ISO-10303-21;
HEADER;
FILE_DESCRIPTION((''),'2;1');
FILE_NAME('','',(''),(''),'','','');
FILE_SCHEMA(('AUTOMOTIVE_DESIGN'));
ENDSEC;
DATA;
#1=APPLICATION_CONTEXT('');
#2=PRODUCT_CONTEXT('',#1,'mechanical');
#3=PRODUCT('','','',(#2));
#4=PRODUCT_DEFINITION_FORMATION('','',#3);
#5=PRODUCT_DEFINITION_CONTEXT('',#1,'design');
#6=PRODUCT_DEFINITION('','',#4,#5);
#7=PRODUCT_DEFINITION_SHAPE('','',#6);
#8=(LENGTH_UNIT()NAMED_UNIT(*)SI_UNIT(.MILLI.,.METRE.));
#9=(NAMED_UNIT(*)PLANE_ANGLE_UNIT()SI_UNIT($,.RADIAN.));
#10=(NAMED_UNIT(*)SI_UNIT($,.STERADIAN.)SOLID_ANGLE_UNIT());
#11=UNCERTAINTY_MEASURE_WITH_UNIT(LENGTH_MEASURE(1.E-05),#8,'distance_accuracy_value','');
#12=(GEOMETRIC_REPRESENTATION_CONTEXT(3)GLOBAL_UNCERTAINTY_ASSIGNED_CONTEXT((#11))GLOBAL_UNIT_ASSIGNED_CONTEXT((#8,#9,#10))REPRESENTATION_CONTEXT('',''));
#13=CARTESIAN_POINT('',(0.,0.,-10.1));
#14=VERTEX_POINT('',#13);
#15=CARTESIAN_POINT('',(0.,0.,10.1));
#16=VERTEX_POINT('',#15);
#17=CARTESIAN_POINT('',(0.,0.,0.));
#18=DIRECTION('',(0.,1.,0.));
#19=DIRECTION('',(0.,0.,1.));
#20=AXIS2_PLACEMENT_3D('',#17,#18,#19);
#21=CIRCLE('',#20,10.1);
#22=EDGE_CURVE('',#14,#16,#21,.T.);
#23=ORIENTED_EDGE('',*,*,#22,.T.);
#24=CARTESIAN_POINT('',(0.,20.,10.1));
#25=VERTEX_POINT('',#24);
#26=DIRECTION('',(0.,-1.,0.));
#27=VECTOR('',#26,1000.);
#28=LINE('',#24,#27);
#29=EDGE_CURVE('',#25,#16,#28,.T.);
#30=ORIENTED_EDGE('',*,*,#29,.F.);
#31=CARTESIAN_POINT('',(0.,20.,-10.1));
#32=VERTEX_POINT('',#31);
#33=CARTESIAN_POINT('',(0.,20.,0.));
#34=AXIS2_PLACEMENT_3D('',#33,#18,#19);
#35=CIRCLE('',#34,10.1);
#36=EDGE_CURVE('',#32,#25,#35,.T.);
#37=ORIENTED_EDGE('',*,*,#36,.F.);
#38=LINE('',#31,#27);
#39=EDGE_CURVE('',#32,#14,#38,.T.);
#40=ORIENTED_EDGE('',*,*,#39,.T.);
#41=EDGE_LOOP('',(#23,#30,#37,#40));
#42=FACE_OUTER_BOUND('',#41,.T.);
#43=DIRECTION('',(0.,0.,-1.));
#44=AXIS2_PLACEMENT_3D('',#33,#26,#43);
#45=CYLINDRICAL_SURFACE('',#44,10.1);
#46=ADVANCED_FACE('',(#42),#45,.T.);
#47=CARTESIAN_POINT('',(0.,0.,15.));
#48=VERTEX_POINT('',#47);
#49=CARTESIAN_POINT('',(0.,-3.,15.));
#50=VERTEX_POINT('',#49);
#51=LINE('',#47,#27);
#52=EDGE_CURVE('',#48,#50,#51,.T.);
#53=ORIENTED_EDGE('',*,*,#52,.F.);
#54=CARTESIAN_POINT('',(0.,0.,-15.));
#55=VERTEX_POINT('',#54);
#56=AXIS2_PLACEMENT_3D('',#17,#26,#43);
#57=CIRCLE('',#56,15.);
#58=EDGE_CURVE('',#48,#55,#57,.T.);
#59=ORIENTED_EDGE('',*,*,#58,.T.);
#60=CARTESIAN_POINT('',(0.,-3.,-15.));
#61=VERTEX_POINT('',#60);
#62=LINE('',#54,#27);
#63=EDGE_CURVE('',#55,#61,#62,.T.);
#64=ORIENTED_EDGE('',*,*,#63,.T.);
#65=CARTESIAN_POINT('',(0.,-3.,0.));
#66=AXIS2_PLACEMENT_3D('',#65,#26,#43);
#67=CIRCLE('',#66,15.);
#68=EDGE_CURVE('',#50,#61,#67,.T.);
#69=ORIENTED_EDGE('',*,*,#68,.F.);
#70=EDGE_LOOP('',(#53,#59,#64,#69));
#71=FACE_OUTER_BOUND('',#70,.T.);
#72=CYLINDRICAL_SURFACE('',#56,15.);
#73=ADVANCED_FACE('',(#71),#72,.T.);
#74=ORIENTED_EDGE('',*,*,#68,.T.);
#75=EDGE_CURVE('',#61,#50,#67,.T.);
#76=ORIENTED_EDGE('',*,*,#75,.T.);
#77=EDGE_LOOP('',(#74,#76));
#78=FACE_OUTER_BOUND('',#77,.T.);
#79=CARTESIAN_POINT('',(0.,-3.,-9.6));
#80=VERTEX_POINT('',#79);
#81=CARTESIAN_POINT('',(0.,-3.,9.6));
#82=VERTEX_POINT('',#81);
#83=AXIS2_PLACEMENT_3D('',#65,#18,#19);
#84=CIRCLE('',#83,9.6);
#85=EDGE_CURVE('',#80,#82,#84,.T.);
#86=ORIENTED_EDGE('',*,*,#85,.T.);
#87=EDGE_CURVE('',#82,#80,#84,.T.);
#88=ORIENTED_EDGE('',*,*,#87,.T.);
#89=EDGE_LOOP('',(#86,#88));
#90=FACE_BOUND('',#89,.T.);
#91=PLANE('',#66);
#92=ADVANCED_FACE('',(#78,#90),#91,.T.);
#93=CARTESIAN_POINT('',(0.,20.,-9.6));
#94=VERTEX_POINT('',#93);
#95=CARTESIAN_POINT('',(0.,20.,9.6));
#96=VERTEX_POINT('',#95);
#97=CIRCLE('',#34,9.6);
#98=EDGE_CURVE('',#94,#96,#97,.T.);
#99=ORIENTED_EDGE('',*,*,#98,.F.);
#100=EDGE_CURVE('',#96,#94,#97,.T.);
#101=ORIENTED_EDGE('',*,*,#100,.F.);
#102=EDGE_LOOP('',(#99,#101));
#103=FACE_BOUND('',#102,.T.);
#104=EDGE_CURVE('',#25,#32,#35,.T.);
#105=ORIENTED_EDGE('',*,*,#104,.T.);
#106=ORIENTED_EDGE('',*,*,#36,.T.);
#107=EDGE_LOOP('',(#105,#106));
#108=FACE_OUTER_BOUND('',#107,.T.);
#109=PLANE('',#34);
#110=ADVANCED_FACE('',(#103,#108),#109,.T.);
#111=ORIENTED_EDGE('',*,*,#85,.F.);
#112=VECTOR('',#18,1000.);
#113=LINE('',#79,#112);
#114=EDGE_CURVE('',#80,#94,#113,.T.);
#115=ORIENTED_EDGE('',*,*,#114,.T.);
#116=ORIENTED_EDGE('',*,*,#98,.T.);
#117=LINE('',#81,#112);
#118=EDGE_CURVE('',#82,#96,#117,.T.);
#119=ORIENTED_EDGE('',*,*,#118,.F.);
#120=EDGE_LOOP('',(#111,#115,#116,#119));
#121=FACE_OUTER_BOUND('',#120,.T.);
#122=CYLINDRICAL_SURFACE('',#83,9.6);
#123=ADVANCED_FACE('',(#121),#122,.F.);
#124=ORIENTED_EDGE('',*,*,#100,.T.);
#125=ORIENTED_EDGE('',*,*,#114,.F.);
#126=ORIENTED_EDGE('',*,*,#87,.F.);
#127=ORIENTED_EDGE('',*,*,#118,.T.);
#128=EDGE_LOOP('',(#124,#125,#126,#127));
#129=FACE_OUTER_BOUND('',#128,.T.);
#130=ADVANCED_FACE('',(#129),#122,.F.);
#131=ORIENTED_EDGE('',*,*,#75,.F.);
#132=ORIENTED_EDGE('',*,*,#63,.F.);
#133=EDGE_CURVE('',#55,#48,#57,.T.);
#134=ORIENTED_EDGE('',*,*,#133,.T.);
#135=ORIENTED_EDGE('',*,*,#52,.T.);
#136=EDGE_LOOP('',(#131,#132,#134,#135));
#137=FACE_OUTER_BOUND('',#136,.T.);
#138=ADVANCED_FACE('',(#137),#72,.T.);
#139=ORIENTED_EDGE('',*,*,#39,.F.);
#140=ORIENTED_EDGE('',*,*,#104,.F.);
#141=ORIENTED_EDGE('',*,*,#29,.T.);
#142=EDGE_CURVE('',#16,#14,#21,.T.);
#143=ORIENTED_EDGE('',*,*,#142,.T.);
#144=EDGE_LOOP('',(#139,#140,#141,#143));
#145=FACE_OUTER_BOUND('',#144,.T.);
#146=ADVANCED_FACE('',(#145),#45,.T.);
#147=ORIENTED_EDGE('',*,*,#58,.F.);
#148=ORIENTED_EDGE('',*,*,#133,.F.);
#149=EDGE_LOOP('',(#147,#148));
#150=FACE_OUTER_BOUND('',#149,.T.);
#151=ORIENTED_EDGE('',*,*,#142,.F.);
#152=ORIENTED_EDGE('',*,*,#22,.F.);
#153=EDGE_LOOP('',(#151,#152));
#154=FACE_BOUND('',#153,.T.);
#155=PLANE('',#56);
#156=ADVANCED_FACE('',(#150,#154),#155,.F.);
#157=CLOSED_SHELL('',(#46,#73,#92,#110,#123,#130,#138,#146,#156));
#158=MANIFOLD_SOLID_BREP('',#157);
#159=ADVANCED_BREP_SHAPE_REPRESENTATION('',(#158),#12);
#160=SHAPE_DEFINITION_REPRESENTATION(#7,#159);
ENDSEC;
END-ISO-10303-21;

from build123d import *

# Parameters (mm, degrees)
SKETCH1_R           = 10.1
BOSS_EXTRUDE1_DEPTH = 20
BOSS_EXTRUDE2_START = 3
SKETCH2_R           = 15
BOSS_EXTRUDE2_DEPTH = 3
SKETCH4_R           = 9.6
CUT_EXTRUDE1_DEPTH  = 32.288975694


with BuildPart() as part:
    # Sketch1 → Boss-Extrude1 (new body)
    with BuildSketch(Plane(origin=(0, 0, 0), x_dir=(1, 0, 0), z_dir=(0, 1, 0))):
        with Locations(Location((0, 0, 0), (0, 0, 270))):
            Circle(SKETCH1_R)
    extrude(amount=BOSS_EXTRUDE1_DEPTH)

    # Sketch2 → Boss-Extrude2 (add)
    with BuildSketch(Plane.XZ.offset(BOSS_EXTRUDE2_START)):
        with Locations(Location((0, 0, 0), (0, 0, 270))):
            Circle(SKETCH2_R)
    extrude(amount=-BOSS_EXTRUDE2_DEPTH)

    # Sketch4 → Cut-Extrude1 (cut, through all)
    with BuildSketch(Plane(origin=(0, 20, 0), x_dir=(1, 0, 0), z_dir=(0, 1, 0))):
        with Locations(Location((0, 0, 0), (0, 0, 270))):
            Circle(SKETCH4_R)
    extrude(amount=-CUT_EXTRUDE1_DEPTH, mode=Mode.SUBTRACT)


solid = part.part
